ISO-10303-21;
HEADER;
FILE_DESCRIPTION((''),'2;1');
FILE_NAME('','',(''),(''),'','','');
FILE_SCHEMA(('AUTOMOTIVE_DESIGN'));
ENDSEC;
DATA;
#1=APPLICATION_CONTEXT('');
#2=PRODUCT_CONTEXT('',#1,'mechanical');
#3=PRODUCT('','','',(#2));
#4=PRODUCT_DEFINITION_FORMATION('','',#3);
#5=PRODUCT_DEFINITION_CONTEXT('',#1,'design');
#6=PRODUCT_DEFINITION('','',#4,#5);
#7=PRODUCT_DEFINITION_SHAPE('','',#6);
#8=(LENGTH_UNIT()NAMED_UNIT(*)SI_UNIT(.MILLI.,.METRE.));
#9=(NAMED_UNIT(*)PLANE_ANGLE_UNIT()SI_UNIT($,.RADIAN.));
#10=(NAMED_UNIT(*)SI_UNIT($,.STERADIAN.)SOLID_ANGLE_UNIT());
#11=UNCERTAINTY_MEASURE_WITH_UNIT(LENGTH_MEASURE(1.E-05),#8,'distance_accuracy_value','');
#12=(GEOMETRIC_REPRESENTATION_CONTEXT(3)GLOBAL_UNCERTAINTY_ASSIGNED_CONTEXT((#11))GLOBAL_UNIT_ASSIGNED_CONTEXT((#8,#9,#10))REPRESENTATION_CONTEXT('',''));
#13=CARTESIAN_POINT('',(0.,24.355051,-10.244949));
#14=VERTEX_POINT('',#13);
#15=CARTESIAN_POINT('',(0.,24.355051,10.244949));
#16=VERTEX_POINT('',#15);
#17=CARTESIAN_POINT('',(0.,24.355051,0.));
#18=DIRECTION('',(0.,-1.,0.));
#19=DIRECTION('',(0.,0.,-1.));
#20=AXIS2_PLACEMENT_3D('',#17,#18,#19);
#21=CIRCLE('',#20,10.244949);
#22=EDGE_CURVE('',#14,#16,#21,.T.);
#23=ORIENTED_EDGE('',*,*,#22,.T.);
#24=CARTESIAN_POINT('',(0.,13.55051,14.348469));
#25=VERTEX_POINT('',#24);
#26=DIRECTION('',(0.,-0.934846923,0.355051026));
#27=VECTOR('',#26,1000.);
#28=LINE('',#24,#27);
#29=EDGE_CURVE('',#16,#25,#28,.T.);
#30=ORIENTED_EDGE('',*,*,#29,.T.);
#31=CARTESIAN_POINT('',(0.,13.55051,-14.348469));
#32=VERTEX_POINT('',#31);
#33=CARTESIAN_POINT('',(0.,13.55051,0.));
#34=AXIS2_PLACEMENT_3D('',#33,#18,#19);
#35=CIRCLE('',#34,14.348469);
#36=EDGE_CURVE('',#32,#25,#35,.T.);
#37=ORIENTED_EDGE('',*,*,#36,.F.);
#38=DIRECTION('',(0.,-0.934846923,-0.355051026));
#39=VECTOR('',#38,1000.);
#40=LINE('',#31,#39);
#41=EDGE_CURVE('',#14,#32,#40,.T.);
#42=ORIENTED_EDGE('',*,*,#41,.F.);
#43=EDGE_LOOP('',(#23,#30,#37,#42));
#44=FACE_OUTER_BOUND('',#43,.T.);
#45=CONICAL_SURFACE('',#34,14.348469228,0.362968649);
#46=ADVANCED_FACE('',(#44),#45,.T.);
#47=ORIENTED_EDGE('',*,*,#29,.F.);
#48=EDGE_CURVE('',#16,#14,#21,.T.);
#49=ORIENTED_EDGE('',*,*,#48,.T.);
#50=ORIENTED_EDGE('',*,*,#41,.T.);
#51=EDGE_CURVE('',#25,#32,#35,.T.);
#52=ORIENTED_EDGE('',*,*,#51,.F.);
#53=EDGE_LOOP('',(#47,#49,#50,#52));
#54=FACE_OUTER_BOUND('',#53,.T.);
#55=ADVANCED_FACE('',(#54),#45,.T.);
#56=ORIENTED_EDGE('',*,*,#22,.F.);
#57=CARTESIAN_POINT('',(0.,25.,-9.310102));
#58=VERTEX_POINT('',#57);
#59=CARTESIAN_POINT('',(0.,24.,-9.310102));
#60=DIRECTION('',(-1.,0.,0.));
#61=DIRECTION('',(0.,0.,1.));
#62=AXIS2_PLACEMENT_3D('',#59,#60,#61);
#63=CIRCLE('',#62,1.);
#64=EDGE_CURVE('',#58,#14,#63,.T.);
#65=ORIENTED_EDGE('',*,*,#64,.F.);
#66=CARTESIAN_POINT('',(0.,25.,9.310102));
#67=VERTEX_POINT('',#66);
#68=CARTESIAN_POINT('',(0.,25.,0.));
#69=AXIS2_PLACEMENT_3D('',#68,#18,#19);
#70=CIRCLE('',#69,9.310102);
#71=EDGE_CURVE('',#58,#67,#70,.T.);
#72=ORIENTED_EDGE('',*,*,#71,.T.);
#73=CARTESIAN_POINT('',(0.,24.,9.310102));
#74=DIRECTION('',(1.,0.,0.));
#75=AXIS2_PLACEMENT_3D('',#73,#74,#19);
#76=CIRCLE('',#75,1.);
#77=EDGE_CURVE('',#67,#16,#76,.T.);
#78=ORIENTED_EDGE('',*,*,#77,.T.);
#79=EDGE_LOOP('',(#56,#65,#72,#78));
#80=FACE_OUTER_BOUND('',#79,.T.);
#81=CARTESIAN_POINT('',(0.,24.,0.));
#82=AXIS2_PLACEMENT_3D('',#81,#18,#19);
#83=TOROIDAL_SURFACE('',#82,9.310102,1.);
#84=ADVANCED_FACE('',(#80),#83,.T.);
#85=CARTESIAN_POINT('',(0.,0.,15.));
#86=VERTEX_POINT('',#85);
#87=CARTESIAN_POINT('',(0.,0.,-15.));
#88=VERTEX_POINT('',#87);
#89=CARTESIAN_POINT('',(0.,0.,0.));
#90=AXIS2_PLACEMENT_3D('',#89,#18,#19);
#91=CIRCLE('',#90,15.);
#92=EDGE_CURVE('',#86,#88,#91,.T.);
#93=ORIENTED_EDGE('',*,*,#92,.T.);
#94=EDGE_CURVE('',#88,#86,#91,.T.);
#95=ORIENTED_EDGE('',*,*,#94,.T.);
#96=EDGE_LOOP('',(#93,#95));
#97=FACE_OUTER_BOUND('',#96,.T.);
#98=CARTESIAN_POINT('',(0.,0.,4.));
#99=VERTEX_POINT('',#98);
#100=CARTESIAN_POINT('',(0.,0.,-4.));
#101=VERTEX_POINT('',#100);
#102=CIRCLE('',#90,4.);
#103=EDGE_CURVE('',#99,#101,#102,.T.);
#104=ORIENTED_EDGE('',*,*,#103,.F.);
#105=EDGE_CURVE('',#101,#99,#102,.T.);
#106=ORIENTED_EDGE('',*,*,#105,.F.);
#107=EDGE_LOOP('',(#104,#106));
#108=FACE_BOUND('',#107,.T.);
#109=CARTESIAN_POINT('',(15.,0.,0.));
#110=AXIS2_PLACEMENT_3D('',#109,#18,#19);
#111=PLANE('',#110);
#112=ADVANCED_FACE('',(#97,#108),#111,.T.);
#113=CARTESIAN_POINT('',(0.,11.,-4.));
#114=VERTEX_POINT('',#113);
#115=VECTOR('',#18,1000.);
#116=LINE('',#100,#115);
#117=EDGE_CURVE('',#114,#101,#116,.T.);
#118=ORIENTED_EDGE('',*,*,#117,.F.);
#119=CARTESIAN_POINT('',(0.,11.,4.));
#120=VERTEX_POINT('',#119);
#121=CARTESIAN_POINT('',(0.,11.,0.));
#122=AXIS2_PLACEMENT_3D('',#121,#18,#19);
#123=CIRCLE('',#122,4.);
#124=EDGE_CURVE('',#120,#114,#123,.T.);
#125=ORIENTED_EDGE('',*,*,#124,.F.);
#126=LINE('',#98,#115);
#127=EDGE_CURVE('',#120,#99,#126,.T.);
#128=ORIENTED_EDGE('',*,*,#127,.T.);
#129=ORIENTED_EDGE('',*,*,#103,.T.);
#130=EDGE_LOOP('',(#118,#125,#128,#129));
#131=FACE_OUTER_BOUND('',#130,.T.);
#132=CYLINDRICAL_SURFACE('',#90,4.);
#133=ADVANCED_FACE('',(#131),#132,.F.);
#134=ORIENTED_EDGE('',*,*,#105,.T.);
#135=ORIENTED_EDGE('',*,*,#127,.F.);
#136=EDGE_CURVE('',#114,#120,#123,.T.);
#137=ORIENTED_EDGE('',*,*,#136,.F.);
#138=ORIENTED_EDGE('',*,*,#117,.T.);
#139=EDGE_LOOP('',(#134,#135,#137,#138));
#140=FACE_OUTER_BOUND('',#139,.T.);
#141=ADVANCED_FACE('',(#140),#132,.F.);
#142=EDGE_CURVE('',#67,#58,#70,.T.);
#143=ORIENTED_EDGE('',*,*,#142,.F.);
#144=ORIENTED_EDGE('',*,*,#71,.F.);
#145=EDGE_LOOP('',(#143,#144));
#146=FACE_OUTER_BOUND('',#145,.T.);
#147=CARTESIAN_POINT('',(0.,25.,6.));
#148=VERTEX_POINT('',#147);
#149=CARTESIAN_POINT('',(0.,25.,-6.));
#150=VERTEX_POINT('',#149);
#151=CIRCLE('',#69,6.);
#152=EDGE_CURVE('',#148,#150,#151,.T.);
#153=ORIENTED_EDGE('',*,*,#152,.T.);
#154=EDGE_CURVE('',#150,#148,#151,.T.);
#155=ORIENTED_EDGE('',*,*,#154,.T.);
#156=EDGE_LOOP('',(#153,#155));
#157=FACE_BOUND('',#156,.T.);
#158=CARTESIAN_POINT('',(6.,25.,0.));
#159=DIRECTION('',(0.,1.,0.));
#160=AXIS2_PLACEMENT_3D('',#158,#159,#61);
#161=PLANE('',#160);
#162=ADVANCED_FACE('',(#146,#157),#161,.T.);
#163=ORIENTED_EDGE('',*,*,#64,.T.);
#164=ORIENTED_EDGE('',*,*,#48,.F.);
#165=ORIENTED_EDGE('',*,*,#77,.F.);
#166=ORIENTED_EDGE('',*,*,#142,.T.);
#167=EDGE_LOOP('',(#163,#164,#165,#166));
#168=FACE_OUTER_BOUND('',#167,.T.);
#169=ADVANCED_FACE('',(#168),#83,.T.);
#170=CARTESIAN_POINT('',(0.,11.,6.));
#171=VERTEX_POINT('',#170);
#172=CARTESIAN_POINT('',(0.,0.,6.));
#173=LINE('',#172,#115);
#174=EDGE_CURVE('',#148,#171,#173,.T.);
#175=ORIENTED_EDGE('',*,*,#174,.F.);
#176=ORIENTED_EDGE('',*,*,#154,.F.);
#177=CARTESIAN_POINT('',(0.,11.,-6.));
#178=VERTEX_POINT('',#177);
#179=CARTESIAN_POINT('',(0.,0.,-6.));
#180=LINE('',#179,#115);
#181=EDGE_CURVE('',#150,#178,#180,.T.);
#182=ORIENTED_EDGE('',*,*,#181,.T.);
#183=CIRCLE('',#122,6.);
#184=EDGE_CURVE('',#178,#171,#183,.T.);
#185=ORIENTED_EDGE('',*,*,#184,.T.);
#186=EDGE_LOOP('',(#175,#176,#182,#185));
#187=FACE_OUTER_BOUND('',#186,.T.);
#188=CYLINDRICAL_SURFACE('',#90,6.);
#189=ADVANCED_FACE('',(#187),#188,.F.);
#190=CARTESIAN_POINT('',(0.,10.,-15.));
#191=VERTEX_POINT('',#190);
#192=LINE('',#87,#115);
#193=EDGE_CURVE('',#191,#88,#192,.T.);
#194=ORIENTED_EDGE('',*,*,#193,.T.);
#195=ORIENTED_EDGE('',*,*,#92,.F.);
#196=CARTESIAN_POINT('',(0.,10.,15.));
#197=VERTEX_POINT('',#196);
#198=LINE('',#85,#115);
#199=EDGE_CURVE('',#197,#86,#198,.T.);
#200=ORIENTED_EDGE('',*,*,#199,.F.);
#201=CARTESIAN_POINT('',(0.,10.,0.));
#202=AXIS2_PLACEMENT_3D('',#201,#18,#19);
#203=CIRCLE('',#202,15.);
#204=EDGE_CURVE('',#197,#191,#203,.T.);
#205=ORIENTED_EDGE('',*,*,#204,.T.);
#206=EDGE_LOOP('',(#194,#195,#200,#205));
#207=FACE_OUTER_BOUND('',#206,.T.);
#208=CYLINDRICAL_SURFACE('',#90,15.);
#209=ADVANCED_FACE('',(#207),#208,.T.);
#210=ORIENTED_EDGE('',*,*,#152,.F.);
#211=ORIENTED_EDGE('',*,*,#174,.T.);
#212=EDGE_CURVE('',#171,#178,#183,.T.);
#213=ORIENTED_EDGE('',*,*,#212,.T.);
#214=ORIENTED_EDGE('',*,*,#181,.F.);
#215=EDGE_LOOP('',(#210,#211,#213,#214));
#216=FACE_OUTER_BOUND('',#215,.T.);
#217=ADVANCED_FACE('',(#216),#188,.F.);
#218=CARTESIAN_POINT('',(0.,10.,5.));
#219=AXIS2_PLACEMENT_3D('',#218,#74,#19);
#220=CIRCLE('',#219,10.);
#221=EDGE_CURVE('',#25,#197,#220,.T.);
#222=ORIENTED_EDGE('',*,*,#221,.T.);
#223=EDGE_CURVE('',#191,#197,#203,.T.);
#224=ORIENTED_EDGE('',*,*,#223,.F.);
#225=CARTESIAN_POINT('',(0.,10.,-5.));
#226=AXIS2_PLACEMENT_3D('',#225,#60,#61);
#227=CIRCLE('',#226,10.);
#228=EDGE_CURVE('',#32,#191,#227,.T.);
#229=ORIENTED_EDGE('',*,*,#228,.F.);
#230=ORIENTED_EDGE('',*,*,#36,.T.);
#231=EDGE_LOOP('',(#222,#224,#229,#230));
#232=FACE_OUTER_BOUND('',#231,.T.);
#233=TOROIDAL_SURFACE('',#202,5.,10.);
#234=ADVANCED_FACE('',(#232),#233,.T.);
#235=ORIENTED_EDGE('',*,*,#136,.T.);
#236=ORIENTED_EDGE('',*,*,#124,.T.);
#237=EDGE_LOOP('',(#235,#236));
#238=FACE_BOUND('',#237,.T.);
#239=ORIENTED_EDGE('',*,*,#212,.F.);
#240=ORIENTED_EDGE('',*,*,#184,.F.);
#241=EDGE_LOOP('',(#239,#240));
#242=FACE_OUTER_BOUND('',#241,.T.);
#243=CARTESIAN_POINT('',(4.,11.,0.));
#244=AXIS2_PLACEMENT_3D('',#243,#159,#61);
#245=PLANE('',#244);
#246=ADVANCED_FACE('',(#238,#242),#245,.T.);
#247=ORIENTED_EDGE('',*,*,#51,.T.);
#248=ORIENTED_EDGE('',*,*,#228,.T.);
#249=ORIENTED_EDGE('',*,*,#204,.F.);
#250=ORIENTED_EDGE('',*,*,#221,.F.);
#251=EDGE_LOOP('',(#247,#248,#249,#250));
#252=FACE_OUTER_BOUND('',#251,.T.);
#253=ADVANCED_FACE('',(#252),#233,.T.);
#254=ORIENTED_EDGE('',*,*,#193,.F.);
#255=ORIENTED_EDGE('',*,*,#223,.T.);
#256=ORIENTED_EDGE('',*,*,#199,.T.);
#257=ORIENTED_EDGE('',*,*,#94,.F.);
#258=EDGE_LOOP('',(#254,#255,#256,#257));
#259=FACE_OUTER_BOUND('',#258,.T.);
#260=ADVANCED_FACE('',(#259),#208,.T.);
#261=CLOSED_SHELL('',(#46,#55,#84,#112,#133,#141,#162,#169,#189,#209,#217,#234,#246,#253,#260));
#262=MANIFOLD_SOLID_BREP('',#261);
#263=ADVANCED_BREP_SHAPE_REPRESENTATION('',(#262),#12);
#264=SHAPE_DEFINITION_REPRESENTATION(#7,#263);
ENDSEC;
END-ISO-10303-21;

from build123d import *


with BuildPart() as part:
    # Sketch1 → Revolve1 (revolve)
    with BuildSketch(Plane.XY, mode=Mode.PRIVATE) as revolve1_sk:
        with BuildLine():
            Line((4, 0), (4, 11))
            Line((4, 11), (6, 11))
            Line((6, 11), (6, 25))
            Line((6, 25), (9.310102051, 25))
            ThreePointArc((9.310102051, 25), (9.877970423, 24.823119379), (10.244948974, 24.355051026))
            Line((10.244948974, 24.355051026), (14.348469228, 13.550510257))
            ThreePointArc((14.348469228, 13.550510257), (14.835768711, 11.804897188), (15, 10))
            Line((15, 10), (15, 0))
            Line((15, 0), (4, 0))
        make_face()
    revolve(revolve1_sk.sketch.rotate(Axis((0, 0, 0), (0, 1, 0)), 90), axis=Axis((0, 0, 0), (0, 1, 0)))


solid = part.part
